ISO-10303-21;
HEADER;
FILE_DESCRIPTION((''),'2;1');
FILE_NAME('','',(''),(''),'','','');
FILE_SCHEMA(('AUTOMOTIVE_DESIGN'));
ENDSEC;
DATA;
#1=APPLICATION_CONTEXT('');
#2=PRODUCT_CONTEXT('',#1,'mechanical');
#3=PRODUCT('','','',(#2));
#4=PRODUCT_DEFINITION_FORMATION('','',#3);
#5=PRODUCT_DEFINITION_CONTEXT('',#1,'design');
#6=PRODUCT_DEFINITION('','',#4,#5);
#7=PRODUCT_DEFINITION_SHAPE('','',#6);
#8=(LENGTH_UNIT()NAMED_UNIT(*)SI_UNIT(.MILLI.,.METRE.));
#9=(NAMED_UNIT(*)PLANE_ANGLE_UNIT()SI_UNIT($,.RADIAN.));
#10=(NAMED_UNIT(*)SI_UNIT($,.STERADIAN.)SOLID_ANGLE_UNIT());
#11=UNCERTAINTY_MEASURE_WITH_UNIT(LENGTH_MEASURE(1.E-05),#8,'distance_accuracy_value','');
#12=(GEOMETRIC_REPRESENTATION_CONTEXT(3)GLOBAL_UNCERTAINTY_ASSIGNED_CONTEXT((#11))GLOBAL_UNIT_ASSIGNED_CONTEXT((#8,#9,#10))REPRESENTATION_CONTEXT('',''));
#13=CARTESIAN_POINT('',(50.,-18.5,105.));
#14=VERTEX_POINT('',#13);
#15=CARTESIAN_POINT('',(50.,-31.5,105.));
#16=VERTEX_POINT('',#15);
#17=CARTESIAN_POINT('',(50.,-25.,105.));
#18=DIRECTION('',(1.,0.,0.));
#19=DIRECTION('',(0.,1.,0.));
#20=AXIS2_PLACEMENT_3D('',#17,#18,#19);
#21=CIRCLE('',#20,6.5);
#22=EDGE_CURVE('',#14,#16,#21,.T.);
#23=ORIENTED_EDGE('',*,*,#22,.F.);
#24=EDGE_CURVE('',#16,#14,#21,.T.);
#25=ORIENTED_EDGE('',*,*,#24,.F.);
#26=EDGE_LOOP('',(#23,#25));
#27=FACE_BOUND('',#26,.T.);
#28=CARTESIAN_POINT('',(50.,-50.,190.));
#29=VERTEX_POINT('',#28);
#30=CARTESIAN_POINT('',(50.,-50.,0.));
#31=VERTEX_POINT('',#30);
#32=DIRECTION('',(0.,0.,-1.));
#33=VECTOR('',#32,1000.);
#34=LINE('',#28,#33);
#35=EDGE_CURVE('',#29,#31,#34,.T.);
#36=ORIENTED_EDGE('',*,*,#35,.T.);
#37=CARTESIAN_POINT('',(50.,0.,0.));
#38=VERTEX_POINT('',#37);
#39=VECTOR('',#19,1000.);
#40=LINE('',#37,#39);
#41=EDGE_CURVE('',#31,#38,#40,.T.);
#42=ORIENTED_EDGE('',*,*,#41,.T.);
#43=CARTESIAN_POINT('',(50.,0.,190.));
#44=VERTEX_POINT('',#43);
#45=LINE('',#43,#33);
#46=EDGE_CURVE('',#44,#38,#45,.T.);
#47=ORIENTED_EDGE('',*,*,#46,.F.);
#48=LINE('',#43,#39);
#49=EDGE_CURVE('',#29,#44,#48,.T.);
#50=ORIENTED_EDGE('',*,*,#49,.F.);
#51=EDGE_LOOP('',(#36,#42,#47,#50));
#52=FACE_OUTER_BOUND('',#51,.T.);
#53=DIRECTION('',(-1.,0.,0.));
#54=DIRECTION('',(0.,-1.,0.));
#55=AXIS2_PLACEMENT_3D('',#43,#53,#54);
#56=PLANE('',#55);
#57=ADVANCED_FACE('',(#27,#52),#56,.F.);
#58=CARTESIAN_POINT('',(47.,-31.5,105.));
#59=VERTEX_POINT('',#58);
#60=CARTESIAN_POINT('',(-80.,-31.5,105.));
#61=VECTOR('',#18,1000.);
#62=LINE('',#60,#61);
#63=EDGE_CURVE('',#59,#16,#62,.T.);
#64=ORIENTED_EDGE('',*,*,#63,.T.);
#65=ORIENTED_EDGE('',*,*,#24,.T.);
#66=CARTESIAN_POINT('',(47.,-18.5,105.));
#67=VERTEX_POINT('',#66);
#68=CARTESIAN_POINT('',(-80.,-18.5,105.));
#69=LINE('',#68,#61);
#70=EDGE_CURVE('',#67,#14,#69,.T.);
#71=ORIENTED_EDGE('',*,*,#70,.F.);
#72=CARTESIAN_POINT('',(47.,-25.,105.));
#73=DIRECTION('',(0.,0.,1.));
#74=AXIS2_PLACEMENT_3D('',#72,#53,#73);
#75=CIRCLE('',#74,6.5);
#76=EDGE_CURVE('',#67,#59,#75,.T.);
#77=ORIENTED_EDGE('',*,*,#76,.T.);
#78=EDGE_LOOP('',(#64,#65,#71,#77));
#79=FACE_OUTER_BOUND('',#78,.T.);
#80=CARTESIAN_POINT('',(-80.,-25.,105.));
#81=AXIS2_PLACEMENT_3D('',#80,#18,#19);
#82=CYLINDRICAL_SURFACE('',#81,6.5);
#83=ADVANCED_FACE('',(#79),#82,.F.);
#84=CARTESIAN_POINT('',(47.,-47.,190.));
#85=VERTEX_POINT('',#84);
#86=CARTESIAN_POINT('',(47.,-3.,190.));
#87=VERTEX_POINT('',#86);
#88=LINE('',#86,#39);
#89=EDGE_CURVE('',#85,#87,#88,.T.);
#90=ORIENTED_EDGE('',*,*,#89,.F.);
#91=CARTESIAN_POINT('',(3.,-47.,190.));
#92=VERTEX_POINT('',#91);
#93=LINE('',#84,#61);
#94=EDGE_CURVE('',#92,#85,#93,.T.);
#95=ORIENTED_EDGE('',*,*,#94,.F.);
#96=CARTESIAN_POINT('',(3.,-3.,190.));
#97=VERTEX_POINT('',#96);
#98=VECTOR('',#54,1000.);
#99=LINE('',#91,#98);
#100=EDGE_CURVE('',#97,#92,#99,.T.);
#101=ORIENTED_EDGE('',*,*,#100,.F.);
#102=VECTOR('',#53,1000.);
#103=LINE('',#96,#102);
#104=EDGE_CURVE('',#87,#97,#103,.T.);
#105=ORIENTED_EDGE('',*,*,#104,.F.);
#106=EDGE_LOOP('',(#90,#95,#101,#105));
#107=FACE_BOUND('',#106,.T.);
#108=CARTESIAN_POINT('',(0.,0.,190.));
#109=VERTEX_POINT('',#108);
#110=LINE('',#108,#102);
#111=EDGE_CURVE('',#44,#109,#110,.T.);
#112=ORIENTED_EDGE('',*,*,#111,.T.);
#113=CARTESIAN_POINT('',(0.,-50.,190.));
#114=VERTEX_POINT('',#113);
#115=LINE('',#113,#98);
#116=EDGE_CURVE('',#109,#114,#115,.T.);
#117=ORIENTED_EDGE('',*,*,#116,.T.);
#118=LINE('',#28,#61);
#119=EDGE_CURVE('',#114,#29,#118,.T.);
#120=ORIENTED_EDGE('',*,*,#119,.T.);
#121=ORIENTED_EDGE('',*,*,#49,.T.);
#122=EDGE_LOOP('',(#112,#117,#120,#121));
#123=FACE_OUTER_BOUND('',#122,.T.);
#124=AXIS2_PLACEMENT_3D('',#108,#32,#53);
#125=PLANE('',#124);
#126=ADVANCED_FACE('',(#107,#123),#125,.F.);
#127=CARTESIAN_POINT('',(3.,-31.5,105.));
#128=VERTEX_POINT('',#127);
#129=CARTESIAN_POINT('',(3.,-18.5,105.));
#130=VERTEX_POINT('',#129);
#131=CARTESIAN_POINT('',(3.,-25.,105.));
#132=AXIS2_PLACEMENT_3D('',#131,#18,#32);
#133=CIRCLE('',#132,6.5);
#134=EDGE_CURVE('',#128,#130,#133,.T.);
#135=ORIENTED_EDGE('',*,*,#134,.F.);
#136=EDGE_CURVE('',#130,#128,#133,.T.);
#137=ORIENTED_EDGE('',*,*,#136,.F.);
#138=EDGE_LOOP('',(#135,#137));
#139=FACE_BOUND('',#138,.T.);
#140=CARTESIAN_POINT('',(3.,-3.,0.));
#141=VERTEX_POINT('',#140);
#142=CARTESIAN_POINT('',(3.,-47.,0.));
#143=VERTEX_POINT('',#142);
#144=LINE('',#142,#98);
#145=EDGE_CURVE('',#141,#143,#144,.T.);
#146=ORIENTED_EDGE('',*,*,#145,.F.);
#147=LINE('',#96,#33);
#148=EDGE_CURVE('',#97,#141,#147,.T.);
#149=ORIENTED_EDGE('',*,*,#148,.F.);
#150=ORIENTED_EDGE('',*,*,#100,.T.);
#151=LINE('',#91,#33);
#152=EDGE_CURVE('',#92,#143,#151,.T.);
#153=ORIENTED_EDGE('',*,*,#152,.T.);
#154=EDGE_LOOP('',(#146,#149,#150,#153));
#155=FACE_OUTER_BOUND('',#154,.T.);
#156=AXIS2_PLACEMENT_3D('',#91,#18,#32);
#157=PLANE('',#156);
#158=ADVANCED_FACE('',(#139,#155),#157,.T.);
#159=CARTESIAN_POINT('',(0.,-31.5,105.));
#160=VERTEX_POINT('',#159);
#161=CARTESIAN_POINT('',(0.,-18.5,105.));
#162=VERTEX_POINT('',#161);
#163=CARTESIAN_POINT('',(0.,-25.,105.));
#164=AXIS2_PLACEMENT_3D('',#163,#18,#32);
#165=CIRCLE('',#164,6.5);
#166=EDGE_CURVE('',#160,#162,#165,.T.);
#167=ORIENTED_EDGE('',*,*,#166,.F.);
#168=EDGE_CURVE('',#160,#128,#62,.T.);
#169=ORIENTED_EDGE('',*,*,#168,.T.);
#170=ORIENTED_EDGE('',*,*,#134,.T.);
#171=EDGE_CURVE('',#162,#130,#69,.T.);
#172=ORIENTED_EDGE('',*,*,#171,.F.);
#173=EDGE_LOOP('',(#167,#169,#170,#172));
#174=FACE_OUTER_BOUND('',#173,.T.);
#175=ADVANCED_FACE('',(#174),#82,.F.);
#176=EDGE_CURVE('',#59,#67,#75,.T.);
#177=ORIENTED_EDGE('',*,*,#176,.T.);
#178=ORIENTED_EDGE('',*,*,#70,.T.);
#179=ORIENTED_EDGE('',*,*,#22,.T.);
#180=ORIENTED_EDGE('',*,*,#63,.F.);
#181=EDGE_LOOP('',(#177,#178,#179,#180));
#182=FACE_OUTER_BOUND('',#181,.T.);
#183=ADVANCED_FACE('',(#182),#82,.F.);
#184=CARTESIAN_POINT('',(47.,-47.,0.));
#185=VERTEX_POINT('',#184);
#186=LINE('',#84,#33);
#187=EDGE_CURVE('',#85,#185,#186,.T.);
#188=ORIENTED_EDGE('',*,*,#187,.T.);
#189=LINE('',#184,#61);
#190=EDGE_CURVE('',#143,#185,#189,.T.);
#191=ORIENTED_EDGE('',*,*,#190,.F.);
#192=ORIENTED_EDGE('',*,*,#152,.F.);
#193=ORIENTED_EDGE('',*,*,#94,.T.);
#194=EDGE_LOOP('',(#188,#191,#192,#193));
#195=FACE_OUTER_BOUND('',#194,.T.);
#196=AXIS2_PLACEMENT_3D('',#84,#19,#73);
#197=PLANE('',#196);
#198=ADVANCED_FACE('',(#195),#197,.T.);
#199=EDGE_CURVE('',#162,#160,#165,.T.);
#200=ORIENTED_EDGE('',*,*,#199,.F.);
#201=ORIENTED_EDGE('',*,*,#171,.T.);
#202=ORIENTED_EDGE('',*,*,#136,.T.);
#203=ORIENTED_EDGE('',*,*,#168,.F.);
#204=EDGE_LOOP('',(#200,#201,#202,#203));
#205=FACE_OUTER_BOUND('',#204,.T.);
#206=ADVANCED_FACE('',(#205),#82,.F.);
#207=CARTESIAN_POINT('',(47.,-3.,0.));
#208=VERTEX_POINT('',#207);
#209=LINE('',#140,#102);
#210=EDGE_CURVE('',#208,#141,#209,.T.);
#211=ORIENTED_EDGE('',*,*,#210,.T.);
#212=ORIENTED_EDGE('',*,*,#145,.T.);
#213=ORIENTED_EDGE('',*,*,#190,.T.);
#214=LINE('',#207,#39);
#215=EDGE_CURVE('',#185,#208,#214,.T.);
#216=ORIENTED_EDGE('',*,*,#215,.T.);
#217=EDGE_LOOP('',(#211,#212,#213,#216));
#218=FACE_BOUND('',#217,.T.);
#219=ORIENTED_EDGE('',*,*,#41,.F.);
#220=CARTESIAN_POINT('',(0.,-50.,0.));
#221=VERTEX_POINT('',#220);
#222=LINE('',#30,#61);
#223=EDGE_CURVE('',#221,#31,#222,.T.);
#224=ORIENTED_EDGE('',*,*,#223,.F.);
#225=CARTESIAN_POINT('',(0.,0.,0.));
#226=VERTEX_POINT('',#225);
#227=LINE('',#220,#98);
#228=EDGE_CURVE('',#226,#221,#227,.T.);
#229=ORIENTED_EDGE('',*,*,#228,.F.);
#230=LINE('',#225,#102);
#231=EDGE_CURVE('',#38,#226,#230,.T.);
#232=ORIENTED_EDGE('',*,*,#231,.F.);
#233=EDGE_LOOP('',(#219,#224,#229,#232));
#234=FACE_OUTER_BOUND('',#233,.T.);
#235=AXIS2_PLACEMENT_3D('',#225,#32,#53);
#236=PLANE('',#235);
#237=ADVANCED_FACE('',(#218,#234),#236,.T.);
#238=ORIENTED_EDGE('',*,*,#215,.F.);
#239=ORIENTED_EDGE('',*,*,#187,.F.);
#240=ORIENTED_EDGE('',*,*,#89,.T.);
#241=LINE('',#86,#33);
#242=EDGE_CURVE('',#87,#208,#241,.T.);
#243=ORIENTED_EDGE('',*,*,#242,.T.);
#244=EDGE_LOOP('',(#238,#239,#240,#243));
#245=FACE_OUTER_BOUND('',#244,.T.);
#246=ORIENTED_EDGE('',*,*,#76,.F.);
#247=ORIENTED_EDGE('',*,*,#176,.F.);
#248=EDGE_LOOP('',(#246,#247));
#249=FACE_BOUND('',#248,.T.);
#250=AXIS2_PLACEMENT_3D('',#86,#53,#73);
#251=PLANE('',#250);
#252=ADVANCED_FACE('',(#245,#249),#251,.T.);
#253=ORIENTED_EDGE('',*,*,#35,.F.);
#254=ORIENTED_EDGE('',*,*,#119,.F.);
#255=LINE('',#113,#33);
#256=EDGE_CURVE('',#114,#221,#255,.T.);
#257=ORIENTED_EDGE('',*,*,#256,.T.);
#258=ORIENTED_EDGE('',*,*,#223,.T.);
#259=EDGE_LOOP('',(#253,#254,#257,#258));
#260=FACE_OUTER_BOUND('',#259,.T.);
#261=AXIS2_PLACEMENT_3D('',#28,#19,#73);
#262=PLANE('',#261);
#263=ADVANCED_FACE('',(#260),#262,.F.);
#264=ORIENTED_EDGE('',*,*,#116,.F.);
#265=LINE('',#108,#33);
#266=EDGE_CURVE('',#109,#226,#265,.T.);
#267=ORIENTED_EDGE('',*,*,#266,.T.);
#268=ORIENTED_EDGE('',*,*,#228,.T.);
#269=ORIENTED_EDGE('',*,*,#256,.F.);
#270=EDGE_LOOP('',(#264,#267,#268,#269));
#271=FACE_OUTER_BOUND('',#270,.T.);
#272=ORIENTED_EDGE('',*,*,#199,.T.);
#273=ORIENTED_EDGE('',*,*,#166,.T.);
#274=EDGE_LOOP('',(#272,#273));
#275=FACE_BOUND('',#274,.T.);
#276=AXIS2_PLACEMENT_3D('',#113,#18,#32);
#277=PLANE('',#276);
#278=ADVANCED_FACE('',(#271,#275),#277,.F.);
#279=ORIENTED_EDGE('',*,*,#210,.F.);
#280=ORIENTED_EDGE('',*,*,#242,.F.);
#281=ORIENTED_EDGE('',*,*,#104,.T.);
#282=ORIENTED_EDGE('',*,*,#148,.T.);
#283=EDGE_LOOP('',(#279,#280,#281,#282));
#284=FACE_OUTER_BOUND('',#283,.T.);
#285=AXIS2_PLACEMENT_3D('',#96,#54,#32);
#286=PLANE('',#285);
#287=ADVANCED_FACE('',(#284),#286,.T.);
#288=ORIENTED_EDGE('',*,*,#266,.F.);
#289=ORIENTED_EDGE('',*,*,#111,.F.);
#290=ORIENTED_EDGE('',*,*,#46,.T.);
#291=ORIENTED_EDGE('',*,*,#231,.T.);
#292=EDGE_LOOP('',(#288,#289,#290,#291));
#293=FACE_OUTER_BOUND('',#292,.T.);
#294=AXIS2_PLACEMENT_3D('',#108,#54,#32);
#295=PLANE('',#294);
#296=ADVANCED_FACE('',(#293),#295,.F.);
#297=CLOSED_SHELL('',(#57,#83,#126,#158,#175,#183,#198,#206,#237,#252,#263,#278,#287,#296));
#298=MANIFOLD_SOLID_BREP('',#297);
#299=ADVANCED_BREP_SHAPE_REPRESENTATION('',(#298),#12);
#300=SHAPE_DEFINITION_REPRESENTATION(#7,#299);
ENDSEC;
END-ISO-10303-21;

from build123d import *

# Parameters (mm, degrees)
SKETCH_1_W          = 50
SKETCH_1_H          = 50
SKETCH_1_W_2        = 44
SKETCH_1_H_2        = 44
EXTRUDE_2_DEPTH     = 190
SKETCH_5_R          = 6.5
CUT_EXTRUDE_1_DEPTH = 130


with BuildPart() as part:
    # 草图1 → 凸台-拉伸2 (new body)
    with BuildSketch(Plane.XY):
        with Locations((25, -25)):
            Rectangle(SKETCH_1_W, SKETCH_1_H)
        with Locations((25, -25)):
            Rectangle(SKETCH_1_W_2, SKETCH_1_H_2, mode=Mode.SUBTRACT)
    extrude(amount=EXTRUDE_2_DEPTH)

    # 草图5 → 切除-拉伸1 (cut)
    with BuildSketch(Plane(origin=(50, 0, 0), x_dir=(0, 0, -1), z_dir=(1, 0, 0))):
        with Locations(Location((-105, -25, 0), (0, 0, 90))):
            Circle(SKETCH_5_R)
        with Locations((-324.839370649, -25)):
            Circle(SKETCH_5_R)
    extrude(amount=-CUT_EXTRUDE_1_DEPTH, mode=Mode.SUBTRACT)


solid = part.part
